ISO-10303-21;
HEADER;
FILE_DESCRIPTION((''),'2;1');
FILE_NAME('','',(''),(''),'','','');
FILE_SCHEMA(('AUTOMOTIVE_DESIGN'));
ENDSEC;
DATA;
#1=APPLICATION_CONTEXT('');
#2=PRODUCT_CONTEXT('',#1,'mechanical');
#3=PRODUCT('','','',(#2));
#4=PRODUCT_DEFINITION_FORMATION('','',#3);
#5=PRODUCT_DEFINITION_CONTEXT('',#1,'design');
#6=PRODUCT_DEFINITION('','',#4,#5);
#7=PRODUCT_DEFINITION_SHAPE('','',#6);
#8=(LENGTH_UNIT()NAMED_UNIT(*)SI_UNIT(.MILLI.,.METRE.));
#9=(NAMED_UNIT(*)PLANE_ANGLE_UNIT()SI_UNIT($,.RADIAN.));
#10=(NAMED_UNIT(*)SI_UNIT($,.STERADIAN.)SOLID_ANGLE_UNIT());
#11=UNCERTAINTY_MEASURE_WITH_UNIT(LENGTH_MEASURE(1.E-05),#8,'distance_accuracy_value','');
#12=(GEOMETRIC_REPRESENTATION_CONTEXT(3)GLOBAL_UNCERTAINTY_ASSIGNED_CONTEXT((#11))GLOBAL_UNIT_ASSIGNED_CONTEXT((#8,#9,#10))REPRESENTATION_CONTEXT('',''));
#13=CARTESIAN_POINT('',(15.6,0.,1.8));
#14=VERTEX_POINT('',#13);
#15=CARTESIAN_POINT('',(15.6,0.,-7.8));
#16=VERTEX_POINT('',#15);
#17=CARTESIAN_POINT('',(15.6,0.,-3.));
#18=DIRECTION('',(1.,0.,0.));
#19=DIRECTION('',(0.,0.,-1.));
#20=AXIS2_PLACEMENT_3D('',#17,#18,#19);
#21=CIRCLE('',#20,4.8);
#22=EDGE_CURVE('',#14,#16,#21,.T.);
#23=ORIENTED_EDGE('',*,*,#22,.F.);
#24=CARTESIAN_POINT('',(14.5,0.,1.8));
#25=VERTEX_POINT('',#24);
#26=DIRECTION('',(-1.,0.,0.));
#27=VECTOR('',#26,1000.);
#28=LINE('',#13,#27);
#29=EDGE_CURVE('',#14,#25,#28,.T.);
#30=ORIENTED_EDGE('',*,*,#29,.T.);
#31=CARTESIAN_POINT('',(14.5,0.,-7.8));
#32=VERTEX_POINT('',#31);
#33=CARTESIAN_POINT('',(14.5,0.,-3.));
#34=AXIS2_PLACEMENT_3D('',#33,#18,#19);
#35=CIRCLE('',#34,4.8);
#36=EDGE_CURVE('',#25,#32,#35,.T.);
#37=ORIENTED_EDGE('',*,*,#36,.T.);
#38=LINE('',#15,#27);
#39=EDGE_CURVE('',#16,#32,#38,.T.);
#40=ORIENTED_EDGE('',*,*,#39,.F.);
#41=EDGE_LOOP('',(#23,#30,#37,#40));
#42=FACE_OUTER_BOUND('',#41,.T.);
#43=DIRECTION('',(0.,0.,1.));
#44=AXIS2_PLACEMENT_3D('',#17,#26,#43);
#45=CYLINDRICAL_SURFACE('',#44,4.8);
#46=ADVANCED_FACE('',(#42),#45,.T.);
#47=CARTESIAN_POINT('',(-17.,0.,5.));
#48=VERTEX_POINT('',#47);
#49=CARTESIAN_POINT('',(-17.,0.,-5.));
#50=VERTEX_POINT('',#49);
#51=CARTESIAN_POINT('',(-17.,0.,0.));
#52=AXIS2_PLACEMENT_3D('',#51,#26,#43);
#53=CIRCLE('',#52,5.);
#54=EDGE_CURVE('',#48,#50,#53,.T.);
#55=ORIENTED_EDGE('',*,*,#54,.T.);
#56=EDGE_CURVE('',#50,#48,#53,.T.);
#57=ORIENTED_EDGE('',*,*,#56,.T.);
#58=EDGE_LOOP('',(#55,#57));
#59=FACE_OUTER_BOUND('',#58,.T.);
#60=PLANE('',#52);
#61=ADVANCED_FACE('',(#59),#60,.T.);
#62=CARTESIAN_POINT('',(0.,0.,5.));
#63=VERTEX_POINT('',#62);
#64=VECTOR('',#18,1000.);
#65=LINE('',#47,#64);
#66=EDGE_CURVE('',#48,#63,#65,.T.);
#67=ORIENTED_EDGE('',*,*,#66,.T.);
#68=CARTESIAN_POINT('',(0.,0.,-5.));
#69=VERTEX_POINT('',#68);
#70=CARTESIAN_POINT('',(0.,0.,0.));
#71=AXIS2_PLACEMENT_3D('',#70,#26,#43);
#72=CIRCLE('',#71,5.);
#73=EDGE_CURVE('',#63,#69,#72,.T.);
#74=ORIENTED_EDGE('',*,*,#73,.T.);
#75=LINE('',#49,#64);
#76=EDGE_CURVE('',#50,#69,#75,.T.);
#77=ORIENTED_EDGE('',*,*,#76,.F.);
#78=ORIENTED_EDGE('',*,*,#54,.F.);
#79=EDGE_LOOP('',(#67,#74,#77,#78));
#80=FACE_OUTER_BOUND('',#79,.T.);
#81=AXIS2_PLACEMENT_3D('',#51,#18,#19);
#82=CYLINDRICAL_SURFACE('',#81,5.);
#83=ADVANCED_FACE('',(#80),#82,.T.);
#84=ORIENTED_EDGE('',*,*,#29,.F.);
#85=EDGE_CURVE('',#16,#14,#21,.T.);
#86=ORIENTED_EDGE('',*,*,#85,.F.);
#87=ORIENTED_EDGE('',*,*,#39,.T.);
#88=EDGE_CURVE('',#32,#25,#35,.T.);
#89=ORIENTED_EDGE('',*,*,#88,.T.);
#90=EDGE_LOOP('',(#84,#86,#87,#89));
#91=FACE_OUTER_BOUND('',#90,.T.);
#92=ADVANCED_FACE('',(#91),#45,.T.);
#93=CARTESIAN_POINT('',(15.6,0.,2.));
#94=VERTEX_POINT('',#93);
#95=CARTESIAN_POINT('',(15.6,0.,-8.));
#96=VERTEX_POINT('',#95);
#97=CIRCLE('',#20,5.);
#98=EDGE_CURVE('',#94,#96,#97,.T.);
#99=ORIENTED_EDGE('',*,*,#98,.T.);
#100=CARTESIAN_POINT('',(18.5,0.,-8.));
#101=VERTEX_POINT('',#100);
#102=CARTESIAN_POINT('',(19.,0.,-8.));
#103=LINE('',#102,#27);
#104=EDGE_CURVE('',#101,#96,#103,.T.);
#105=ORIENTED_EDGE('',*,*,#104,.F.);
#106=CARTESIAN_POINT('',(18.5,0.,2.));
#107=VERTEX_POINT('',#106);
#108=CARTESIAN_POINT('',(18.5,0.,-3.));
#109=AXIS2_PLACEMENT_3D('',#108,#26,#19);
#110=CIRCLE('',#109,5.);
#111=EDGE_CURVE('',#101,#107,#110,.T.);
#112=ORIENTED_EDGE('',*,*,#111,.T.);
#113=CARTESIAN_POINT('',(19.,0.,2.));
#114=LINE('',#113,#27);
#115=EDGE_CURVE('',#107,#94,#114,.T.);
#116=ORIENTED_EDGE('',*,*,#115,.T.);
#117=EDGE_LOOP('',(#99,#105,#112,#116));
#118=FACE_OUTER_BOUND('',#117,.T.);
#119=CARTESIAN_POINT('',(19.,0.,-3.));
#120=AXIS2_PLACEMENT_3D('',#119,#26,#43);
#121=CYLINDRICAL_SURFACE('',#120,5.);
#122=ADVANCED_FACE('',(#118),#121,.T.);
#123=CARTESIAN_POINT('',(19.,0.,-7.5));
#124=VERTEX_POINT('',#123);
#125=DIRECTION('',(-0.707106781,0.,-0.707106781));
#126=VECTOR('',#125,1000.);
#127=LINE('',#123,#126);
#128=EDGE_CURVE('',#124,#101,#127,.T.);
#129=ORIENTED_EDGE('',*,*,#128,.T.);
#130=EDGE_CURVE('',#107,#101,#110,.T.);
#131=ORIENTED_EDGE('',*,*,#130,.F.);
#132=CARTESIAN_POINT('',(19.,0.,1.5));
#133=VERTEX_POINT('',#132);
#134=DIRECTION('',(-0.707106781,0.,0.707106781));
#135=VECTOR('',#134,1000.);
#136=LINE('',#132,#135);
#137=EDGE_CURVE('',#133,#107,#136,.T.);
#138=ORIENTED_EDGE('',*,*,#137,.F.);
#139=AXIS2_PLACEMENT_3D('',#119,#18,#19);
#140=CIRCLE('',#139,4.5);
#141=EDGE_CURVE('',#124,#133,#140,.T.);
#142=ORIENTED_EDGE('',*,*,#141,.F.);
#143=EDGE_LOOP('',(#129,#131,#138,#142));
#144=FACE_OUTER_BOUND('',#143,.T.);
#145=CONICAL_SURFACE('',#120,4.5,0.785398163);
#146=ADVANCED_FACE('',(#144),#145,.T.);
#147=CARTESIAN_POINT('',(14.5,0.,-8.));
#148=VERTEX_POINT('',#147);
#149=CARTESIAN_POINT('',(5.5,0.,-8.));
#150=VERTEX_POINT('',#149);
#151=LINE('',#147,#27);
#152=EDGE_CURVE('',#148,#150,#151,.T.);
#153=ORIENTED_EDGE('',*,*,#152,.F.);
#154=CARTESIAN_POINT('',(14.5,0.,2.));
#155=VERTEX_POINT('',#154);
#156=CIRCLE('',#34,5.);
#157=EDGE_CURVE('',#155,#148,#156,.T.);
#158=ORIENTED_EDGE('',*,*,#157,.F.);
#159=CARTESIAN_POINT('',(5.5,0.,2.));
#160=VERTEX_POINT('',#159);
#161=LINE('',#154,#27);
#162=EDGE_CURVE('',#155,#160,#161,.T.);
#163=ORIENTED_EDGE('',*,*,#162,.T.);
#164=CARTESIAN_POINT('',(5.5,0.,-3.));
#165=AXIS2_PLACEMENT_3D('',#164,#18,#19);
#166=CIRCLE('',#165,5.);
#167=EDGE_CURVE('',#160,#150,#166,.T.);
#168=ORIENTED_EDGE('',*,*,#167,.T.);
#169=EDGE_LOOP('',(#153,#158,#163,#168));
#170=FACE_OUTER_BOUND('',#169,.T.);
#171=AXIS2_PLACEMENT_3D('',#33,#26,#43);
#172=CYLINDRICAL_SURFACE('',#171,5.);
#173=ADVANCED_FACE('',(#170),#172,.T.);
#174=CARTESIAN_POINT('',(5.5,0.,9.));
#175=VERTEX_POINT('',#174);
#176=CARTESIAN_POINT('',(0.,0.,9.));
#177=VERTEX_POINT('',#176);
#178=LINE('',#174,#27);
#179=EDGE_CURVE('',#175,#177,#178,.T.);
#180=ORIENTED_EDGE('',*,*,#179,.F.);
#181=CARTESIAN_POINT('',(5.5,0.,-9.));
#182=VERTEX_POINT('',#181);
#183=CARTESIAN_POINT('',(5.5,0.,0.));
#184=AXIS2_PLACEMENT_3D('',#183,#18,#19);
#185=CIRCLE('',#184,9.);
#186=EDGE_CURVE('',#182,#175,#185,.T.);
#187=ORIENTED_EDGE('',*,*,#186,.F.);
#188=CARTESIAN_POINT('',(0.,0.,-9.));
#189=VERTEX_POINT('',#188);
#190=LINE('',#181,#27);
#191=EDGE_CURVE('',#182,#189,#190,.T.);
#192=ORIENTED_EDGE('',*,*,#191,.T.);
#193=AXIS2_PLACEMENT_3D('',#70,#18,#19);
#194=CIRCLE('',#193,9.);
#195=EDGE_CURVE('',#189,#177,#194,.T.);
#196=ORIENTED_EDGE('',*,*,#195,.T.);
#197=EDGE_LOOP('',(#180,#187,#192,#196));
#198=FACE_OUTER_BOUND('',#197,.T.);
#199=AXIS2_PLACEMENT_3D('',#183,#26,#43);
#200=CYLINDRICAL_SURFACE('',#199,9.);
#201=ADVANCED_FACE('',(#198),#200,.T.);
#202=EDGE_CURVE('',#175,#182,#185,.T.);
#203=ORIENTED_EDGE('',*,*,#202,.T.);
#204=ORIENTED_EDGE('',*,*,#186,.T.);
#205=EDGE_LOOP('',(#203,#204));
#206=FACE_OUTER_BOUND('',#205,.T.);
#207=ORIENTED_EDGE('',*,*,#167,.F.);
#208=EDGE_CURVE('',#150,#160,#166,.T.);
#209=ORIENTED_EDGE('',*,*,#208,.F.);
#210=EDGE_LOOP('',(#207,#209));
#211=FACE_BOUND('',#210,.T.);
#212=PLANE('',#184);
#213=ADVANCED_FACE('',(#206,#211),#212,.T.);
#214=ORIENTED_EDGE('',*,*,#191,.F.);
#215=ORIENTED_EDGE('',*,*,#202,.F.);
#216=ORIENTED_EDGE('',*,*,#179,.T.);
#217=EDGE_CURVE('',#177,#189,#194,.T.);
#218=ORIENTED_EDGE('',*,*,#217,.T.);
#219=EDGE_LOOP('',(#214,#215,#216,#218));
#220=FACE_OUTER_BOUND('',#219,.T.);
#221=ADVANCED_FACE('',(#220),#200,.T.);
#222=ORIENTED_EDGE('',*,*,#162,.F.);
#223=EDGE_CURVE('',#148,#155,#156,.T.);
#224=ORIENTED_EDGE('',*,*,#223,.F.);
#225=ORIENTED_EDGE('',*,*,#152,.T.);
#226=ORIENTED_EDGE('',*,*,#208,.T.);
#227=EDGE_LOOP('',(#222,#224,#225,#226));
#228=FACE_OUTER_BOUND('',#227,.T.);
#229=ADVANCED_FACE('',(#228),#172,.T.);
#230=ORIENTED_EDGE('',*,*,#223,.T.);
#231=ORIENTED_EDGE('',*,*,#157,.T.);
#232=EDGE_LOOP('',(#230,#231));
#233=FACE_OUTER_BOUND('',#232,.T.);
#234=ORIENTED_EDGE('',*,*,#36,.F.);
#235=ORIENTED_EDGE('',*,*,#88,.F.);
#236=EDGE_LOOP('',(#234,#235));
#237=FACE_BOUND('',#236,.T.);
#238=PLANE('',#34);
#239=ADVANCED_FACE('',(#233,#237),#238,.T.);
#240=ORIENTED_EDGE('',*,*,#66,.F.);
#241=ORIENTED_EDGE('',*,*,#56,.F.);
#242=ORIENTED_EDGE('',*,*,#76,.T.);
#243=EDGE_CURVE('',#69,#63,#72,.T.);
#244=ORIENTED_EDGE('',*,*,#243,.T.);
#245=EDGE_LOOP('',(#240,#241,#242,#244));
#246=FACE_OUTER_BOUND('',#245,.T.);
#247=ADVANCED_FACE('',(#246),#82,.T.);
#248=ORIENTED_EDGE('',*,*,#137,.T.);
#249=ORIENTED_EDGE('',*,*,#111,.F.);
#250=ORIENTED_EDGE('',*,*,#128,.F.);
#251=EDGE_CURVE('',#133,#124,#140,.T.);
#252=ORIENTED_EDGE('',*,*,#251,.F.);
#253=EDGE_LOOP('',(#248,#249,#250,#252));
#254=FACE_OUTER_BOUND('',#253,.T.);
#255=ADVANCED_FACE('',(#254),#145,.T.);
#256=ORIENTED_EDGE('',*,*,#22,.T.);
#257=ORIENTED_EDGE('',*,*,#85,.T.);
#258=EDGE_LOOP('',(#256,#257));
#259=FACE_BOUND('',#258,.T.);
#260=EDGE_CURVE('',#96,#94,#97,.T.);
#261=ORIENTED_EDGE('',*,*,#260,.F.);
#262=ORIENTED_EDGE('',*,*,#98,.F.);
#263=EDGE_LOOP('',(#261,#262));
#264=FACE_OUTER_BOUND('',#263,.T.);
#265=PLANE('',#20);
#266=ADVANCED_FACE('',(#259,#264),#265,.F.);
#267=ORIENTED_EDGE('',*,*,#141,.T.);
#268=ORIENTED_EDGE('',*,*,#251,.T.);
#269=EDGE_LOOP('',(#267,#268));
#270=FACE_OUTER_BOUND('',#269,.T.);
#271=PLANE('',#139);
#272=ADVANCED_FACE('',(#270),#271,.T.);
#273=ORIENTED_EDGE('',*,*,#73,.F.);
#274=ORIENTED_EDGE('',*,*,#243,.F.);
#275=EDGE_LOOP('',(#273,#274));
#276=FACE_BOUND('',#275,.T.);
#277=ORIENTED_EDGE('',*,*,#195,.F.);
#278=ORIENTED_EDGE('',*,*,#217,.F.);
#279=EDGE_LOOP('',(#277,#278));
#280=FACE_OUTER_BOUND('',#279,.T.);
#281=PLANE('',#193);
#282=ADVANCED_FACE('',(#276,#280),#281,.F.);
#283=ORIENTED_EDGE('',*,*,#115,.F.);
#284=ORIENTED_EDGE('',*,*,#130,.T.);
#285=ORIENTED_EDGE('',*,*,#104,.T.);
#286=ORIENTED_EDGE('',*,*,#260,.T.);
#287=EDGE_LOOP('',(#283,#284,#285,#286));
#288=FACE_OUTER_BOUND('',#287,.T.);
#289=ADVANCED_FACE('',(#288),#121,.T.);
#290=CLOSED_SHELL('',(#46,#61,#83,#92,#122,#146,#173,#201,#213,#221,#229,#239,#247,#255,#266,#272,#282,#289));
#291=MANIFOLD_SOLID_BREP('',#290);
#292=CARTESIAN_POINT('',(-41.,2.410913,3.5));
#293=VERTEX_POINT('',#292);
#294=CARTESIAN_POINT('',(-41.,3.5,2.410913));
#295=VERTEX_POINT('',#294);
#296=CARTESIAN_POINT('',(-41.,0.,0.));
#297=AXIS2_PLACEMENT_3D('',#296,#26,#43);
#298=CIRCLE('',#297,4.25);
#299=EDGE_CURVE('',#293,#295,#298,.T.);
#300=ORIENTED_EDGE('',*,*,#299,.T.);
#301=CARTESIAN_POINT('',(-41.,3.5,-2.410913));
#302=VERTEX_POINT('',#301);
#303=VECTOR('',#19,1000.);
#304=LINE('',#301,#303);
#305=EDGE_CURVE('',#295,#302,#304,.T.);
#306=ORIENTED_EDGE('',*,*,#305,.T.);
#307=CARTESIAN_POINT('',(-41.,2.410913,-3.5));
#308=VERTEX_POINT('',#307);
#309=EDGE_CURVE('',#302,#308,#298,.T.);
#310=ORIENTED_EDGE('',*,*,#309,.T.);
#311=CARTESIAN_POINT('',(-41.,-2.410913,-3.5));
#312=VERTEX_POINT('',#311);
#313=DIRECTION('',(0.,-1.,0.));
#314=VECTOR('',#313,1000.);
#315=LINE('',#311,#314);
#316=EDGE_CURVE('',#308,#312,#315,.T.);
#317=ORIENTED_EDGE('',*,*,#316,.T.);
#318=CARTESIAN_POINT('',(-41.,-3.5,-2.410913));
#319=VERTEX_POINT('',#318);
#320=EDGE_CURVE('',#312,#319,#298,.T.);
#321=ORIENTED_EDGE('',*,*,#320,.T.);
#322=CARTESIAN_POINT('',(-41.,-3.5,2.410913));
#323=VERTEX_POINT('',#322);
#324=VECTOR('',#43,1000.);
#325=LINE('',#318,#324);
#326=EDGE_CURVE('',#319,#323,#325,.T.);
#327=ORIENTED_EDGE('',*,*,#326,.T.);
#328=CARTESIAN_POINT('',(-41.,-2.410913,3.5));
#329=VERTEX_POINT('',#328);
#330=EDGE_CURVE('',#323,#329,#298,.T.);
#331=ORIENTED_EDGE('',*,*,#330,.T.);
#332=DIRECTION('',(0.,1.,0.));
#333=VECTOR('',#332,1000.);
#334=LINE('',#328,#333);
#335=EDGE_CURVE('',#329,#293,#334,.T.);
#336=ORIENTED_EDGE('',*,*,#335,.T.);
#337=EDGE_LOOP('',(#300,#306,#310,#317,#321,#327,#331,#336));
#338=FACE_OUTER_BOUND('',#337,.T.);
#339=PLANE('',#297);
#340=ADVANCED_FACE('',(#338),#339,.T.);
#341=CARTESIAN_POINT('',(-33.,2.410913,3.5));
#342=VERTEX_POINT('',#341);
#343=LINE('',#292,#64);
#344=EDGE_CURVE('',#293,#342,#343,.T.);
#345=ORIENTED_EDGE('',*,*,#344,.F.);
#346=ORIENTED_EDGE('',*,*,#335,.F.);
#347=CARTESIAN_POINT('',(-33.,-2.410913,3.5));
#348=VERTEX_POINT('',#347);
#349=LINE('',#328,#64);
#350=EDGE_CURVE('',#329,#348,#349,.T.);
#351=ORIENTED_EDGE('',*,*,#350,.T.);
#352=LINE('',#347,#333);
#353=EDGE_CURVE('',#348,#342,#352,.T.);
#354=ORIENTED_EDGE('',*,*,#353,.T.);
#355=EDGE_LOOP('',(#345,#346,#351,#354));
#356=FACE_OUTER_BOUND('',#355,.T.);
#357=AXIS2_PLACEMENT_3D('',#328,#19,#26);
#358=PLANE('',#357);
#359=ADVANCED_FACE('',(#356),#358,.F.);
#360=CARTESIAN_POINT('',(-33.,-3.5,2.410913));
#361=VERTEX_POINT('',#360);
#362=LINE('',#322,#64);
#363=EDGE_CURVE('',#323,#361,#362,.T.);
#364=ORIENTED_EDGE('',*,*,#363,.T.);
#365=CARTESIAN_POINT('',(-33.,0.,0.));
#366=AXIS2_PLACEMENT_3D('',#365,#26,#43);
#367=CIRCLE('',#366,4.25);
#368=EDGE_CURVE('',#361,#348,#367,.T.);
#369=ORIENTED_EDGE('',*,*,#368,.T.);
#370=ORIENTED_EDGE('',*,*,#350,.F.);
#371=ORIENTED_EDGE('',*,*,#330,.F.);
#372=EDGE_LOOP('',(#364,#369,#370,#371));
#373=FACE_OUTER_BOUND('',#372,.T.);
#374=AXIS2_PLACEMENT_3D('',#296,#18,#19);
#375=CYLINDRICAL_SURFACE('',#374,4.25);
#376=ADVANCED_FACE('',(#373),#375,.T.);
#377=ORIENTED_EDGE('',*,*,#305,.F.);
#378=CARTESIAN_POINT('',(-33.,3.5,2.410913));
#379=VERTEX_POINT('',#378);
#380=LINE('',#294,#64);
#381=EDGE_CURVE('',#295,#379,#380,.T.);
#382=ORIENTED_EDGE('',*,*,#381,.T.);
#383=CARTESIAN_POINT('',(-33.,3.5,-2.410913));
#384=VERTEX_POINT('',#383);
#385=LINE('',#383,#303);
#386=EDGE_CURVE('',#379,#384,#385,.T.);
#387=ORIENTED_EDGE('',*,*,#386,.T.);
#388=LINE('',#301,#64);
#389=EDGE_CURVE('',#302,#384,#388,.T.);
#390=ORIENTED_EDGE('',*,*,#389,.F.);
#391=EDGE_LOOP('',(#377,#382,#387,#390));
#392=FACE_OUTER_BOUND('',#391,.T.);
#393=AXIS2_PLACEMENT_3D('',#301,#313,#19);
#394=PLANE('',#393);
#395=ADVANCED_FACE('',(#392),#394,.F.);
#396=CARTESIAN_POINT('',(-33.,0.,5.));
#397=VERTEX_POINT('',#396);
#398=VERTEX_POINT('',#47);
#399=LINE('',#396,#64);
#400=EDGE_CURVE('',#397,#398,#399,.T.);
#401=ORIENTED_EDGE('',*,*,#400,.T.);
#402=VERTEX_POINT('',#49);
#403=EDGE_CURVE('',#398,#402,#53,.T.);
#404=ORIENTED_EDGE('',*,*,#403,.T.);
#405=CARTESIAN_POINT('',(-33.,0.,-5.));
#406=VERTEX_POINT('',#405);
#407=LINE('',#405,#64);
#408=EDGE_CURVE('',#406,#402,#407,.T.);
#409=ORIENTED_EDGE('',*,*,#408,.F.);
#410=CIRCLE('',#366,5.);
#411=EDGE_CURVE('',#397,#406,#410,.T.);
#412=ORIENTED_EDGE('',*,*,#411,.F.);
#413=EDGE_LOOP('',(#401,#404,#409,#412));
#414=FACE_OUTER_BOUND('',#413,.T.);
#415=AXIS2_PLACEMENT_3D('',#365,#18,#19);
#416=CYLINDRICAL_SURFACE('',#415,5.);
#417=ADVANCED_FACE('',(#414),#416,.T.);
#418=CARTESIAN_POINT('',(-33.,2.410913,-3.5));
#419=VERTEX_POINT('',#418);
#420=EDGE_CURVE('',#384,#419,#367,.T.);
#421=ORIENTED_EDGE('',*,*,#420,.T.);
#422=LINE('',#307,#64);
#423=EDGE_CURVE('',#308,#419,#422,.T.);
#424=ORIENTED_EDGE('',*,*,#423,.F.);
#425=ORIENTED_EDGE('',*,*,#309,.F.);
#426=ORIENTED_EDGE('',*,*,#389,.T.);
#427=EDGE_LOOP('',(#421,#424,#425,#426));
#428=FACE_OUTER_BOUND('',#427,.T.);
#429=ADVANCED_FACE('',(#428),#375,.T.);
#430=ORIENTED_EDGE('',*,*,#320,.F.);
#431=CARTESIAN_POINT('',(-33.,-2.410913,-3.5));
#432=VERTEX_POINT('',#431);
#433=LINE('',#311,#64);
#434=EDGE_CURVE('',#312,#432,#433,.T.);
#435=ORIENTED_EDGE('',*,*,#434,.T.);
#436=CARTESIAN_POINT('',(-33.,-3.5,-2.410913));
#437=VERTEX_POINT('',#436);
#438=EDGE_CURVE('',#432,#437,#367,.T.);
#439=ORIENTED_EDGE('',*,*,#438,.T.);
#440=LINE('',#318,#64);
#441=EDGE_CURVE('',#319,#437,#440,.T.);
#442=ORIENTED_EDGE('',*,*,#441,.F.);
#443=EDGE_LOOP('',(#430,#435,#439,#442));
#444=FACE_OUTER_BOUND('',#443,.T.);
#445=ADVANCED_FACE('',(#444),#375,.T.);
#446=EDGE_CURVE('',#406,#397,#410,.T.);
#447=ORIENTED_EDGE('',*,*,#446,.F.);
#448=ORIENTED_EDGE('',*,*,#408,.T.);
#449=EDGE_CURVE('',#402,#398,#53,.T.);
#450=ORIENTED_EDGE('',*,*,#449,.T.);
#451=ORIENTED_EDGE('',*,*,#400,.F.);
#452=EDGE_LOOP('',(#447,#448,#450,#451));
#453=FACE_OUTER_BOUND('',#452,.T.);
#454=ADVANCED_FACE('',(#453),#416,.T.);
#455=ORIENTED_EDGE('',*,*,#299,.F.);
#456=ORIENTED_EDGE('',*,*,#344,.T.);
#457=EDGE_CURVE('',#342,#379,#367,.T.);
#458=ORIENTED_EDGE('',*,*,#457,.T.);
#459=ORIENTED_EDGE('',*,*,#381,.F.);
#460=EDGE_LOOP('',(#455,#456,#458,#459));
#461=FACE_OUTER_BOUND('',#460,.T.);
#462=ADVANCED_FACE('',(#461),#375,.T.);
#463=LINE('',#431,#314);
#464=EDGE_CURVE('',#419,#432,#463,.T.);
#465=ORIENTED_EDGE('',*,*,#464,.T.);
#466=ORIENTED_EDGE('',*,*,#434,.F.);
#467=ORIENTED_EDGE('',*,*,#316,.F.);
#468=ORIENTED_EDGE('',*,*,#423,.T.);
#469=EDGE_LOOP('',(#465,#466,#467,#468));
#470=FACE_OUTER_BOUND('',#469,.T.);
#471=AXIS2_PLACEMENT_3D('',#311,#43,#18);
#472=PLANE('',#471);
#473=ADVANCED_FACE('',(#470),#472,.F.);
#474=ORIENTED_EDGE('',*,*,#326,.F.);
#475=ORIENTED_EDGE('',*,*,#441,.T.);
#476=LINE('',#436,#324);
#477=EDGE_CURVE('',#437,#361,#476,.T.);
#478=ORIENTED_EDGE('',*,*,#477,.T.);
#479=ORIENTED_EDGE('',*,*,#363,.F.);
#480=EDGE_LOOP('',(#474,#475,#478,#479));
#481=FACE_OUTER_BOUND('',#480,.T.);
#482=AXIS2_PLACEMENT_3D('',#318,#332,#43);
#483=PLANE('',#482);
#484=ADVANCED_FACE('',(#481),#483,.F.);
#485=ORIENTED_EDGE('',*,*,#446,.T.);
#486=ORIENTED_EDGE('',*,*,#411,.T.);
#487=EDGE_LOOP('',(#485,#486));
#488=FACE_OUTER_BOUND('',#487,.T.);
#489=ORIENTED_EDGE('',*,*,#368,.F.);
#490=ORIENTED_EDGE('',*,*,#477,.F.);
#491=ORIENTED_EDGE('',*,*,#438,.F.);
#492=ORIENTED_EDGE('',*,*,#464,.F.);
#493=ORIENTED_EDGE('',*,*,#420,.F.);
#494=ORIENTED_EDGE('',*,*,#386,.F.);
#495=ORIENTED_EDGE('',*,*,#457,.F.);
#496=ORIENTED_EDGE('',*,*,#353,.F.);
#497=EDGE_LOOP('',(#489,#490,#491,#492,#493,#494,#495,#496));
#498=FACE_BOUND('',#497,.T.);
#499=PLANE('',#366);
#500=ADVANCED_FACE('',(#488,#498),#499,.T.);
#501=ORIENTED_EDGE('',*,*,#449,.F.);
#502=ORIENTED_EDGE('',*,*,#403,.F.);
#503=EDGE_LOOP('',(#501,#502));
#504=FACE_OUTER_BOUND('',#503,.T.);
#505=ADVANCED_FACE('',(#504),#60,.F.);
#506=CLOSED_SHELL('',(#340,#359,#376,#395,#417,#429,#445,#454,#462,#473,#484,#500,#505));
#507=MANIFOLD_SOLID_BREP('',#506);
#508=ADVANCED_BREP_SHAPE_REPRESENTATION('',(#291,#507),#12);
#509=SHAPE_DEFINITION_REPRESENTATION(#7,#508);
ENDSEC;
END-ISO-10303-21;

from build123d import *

# Parameters (mm, degrees)
SKETCH_2_R      = 9
EXTRUDE_1_DEPTH = 5.5
SKETCH_3_R      = 5
EXTRUDE_2_DEPTH = 9
SKETCH_4_R      = 4.8
EXTRUDE_3_DEPTH = 1.1
SKETCH_5_R      = 5
EXTRUDE_4_DEPTH = 3.4
CHAMFER_1_SIZE  = 0.5
SKETCH_6_R      = 5
EXTRUDE_5_DEPTH = 17
SKETCH_7_R      = 5
EXTRUDE_6_DEPTH = 16
EXTRUDE_7_DEPTH = 8


with BuildPart() as part:
    # 草图2 → 凸台-拉伸1 (new body)
    with BuildSketch(Plane(origin=(0, 0, 0), x_dir=(0, 0, -1), z_dir=(1, 0, 0))):
        Circle(SKETCH_2_R)
    extrude(amount=EXTRUDE_1_DEPTH)

    # 草图3 → 凸台-拉伸2 (add)
    with BuildSketch(Plane(origin=(5.5, 0, 0), x_dir=(0, 0, -1), z_dir=(1, 0, 0))):
        with Locations((3, 0)):
            Circle(SKETCH_3_R)
    extrude(amount=EXTRUDE_2_DEPTH)

    # 草图4 → 凸台-拉伸3 (add)
    with BuildSketch(Plane(origin=(14.5, 0, 0), x_dir=(0, 0, -1), z_dir=(1, 0, 0))):
        with Locations((3, 0)):
            Circle(SKETCH_4_R)
    extrude(amount=EXTRUDE_3_DEPTH)

    # 草图5 → 凸台-拉伸4 (add)
    with BuildSketch(Plane(origin=(15.6, 0, 0), x_dir=(0, 0, -1), z_dir=(1, 0, 0))):
        with Locations((3, 0)):
            Circle(SKETCH_5_R)
    extrude(amount=EXTRUDE_4_DEPTH)

    # 倒角1
    chamfer_1_edges = [part.edges().sort_by_distance(p)[0] for p in [
        (19, 0, 2),
    ]]
    chamfer(chamfer_1_edges, length=CHAMFER_1_SIZE)

    # 草图6 → 凸台-拉伸5 (add)
    with BuildSketch(Plane.ZY):
        Circle(SKETCH_6_R)
    extrude(amount=EXTRUDE_5_DEPTH)


with BuildPart() as body_2:
    # 草图7 → 凸台-拉伸6 (new body)
    with BuildSketch(Plane.ZY.offset(17)):
        Circle(SKETCH_7_R)
    extrude(amount=EXTRUDE_6_DEPTH)

    # 草图8 → 凸台-拉伸7 (add)
    with BuildSketch(Plane.ZY.offset(33)):
        with BuildLine():
            Line((-2.41091269, -3.5), (2.41091269, -3.5))
            ThreePointArc((2.41091269, -3.5), (3.00520382, -3.00520382), (3.5, -2.41091269))
            Line((3.5, -2.41091269), (3.5, 2.41091269))
            ThreePointArc((3.5, 2.41091269), (3.00520382, 3.00520382), (2.41091269, 3.5))
            Line((2.41091269, 3.5), (-2.41091269, 3.5))
            ThreePointArc((-2.41091269, 3.5), (-3.00520382, 3.00520382), (-3.5, 2.41091269))
            Line((-3.5, 2.41091269), (-3.5, -2.41091269))
            ThreePointArc((-3.5, -2.41091269), (-3.00520382, -3.00520382), (-2.41091269, -3.5))
        make_face()
    extrude(amount=EXTRUDE_7_DEPTH)


solid = Compound([part.part, body_2.part])
